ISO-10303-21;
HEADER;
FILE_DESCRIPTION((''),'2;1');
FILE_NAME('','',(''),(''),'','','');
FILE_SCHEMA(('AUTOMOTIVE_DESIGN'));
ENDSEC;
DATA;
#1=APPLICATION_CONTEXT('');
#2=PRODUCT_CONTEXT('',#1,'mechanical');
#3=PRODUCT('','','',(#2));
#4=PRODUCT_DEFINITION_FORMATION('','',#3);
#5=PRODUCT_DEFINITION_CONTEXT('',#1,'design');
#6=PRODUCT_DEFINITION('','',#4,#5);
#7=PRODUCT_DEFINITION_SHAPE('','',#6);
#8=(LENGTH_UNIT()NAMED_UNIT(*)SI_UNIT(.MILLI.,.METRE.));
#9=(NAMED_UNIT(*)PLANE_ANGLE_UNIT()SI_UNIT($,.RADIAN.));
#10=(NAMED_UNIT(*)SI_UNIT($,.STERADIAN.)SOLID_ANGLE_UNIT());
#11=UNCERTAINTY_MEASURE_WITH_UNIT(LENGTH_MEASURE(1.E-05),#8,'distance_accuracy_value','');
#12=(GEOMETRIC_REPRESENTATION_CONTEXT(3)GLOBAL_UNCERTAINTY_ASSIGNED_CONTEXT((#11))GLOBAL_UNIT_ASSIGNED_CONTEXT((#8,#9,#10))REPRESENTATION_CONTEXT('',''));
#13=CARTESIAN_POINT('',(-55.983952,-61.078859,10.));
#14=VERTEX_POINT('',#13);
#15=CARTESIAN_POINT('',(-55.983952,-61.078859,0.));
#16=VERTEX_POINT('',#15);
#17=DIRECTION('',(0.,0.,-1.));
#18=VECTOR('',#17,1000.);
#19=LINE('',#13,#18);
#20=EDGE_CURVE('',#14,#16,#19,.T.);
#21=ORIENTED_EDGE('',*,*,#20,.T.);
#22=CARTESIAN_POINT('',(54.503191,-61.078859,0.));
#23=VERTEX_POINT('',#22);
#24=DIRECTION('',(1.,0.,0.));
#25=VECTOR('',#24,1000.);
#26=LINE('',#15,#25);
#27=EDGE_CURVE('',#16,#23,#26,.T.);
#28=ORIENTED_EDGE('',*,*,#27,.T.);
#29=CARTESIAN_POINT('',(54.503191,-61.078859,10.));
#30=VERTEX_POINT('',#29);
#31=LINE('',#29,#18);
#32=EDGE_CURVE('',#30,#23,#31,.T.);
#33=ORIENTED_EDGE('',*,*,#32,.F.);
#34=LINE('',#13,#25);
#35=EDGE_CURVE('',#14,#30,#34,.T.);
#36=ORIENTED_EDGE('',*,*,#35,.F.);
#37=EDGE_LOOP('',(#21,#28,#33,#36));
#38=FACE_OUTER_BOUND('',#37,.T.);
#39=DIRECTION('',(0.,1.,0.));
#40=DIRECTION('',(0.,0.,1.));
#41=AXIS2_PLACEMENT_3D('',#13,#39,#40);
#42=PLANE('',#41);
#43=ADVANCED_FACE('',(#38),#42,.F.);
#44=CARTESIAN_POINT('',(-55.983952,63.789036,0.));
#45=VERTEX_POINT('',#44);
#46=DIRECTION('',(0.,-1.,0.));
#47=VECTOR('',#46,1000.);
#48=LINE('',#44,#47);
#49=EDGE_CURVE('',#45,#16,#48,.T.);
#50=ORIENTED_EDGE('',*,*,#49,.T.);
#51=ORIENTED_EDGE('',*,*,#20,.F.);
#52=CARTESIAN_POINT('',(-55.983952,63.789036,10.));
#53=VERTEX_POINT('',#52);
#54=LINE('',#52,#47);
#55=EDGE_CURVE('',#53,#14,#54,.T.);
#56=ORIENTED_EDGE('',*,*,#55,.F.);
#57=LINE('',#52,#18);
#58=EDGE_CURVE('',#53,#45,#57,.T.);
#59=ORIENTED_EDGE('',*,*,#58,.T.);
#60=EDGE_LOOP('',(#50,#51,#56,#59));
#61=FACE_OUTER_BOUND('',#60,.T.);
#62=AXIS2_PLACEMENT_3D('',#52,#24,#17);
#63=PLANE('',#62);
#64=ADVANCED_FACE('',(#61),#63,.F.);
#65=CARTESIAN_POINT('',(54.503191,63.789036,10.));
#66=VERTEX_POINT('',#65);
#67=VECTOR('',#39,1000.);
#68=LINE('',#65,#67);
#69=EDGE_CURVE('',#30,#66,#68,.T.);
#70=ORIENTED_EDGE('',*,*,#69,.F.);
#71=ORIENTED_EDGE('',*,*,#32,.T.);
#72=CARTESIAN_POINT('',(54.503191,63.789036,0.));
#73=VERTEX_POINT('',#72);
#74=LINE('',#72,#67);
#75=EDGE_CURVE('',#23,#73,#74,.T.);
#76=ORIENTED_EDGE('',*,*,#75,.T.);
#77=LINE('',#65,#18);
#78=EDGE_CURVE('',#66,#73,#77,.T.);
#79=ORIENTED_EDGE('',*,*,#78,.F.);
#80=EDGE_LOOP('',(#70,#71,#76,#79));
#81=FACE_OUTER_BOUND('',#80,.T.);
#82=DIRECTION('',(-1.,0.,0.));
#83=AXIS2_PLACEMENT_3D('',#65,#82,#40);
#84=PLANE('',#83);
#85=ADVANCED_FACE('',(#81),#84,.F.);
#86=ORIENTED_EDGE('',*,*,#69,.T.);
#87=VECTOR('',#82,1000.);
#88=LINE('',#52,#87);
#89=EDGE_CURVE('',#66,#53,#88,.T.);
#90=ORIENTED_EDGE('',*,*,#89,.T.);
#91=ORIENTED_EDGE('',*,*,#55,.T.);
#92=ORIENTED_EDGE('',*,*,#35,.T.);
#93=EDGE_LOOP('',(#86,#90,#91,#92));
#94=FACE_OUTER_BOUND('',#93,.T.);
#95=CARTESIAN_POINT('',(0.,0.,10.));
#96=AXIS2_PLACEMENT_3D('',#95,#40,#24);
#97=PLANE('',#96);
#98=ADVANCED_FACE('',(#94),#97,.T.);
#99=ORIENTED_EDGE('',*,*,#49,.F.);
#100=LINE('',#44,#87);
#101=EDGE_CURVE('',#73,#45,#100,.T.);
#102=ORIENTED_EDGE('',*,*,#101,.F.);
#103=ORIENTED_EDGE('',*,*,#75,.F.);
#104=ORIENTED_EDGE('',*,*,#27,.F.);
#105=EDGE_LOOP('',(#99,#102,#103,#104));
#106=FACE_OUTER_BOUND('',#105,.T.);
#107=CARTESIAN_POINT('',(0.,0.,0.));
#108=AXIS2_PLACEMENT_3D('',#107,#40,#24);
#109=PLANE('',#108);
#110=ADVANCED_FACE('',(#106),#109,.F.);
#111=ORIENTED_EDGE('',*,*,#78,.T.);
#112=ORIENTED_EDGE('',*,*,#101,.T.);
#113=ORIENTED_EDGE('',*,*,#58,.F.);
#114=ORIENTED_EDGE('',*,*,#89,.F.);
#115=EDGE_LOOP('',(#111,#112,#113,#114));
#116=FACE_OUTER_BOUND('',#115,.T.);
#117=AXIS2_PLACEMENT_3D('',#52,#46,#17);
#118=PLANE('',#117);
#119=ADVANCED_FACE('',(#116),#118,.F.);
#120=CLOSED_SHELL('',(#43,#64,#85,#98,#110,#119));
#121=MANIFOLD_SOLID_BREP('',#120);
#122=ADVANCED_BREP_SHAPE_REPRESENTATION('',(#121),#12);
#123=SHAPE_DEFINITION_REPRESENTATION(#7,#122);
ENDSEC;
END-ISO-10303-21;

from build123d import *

# Parameters (mm, degrees)
SKETCH1_W           = 110.487143692
SKETCH1_H           = 124.867894346
BOSS_EXTRUDE1_DEPTH = 10


with BuildPart() as part:
    # Sketch1 → Boss-Extrude1 (new body)
    with BuildSketch(Plane.XY):
        with Locations((-0.740380611, 1.355088617)):
            Rectangle(SKETCH1_W, SKETCH1_H)
    extrude(amount=BOSS_EXTRUDE1_DEPTH)


solid = part.part
